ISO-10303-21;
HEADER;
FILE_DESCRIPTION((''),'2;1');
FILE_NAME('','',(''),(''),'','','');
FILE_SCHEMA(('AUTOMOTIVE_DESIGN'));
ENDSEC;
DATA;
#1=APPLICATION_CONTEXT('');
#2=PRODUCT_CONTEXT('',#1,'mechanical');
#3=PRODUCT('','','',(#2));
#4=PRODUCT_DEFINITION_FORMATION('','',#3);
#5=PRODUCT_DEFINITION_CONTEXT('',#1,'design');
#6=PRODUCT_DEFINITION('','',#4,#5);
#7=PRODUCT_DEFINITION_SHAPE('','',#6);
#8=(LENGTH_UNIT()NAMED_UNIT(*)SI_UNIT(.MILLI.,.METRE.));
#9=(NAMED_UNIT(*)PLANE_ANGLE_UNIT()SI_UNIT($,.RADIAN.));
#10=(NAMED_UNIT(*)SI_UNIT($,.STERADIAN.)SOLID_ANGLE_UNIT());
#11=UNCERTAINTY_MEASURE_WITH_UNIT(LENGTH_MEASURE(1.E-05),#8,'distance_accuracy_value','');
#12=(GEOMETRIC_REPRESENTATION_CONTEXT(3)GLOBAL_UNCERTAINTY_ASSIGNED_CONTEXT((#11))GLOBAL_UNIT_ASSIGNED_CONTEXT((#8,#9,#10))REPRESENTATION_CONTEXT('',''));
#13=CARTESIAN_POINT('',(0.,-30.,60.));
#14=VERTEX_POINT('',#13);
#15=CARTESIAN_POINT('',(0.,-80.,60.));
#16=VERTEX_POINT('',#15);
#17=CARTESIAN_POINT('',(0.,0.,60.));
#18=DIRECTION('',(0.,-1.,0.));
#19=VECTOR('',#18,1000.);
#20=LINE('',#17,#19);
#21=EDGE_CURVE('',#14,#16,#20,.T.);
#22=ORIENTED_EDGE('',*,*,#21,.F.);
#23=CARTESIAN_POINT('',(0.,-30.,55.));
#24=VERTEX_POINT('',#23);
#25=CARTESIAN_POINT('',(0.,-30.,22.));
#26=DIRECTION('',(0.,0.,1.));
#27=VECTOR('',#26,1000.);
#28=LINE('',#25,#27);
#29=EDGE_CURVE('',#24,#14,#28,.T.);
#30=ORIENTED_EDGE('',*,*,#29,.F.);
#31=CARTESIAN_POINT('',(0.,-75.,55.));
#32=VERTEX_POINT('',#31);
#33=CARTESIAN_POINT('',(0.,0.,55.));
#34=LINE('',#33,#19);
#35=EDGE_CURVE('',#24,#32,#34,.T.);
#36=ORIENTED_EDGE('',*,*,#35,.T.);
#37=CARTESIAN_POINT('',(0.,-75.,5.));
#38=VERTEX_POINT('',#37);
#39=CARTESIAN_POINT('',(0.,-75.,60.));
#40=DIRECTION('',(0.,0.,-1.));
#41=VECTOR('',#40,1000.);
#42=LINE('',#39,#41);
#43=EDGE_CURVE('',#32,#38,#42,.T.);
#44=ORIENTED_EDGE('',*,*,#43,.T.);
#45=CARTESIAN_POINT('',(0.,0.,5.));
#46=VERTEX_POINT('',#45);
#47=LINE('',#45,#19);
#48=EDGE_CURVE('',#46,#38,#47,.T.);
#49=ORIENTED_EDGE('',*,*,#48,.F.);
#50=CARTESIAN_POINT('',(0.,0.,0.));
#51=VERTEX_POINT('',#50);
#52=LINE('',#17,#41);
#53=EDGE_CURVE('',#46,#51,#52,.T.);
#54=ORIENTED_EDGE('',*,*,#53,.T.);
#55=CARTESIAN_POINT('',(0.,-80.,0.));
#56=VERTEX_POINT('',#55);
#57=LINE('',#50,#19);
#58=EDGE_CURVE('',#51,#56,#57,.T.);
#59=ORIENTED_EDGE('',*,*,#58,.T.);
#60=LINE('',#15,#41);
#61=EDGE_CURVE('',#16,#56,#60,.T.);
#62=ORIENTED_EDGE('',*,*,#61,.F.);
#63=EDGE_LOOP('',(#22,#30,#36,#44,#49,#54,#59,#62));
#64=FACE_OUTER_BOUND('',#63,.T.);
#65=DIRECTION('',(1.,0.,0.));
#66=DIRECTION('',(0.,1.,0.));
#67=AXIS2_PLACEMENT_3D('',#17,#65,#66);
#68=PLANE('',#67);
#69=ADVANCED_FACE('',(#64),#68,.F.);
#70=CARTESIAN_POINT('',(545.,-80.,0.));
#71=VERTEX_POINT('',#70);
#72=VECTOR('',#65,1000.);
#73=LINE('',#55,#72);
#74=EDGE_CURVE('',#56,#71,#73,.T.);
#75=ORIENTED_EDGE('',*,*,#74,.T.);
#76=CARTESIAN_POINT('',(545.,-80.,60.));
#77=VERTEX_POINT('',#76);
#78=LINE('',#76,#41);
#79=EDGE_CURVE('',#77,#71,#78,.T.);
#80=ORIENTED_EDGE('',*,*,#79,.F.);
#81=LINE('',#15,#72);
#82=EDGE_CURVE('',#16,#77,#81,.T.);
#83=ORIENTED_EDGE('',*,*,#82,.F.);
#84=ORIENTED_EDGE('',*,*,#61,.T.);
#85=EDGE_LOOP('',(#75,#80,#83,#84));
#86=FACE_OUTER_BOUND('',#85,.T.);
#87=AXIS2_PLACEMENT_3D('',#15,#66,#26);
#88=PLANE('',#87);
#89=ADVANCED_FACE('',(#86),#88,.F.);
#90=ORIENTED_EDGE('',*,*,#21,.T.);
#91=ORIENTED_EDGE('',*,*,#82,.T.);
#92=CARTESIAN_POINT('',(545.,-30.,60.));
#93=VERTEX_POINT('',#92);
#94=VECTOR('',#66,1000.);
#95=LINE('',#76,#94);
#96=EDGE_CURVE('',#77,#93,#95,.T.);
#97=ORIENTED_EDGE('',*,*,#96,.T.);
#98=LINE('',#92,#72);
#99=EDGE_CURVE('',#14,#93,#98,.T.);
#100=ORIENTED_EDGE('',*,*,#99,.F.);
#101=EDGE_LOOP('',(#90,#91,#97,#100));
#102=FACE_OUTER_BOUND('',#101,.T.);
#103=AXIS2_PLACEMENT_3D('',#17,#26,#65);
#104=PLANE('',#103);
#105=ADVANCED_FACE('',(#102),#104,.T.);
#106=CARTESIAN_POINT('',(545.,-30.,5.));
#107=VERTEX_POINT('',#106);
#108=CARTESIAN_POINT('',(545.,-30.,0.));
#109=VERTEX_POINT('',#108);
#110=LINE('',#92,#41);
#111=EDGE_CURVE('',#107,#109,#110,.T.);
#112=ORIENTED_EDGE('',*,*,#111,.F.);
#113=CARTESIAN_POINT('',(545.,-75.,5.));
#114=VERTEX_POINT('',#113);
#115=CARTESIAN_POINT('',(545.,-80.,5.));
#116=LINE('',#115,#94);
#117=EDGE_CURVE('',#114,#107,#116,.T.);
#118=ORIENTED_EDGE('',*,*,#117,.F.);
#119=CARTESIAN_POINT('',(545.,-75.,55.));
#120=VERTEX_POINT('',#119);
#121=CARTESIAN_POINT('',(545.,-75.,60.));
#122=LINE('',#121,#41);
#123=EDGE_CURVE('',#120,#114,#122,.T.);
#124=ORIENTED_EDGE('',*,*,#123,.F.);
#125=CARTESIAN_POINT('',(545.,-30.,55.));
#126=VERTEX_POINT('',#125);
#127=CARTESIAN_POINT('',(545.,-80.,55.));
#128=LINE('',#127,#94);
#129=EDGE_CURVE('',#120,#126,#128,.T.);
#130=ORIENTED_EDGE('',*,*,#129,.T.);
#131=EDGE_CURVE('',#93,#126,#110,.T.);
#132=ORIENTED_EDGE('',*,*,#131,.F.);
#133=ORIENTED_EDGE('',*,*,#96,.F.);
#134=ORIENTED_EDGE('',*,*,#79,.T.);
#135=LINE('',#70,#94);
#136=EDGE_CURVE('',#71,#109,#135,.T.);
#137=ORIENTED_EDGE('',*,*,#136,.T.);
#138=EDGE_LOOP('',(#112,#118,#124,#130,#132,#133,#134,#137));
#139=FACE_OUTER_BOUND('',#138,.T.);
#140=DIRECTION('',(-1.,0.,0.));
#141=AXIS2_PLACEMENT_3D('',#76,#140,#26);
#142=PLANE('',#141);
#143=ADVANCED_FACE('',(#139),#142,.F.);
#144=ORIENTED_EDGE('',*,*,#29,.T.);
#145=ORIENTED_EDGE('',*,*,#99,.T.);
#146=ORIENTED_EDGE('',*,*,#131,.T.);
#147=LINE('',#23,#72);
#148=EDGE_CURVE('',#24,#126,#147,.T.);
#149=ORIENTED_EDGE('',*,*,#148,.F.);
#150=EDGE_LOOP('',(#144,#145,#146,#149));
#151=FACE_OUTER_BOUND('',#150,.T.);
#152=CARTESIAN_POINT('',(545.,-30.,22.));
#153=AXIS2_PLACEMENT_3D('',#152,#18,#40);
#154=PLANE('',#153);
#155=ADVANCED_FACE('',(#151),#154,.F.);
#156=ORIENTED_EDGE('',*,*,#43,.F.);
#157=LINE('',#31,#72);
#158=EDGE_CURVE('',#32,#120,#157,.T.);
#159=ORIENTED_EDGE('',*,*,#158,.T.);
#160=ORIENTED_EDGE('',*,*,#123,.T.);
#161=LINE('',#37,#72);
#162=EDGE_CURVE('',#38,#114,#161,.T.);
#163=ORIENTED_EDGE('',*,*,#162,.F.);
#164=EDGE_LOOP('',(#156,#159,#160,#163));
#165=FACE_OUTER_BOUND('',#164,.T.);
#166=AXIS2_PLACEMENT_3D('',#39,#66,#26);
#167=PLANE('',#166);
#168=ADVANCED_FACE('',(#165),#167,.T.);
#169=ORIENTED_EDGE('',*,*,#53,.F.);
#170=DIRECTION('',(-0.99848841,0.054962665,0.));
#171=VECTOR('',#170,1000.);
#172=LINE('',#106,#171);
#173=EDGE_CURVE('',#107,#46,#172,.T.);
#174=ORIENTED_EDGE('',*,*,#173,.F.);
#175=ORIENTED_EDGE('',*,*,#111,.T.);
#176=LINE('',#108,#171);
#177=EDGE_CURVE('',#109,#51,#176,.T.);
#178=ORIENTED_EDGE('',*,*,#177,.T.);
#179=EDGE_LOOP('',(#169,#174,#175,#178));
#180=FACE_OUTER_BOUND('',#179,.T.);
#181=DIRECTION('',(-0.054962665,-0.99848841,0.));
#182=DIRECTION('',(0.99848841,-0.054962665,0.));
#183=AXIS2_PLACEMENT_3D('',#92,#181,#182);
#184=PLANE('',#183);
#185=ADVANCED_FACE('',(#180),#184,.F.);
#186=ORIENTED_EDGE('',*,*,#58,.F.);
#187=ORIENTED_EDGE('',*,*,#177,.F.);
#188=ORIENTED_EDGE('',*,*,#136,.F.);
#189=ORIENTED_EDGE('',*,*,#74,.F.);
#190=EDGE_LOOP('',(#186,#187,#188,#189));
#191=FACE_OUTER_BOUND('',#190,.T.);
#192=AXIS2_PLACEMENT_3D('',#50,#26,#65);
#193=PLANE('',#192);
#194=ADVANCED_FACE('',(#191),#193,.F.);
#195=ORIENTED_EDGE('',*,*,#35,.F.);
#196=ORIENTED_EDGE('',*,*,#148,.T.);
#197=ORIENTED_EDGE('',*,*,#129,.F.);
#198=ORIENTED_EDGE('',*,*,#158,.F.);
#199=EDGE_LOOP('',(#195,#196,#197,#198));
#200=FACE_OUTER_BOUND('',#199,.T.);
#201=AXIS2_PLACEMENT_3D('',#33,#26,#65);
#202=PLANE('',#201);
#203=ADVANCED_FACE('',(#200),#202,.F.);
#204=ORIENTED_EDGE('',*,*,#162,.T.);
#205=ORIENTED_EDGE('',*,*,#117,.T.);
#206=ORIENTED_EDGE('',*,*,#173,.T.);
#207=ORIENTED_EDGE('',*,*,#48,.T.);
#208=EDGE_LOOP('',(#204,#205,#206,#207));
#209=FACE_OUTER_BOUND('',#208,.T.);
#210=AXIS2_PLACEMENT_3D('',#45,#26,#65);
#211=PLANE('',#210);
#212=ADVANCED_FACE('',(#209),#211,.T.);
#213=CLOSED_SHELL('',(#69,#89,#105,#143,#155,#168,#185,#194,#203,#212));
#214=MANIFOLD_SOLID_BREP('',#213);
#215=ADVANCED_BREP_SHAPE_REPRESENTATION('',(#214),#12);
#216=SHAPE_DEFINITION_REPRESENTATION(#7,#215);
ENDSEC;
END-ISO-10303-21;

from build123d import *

# Parameters (mm, degrees)
EXTRUDE_1_DEPTH     = 60
SHELL_2_T           = -5
CUT_EXTRUDE_2_DEPTH = 38


with BuildPart() as part:
    # 草图1 → 凸台-拉伸1 (new body)
    with BuildSketch(Plane.XY):
        Polygon((0, 0), (0, -80), (545, -80), (545, -30), align=None)
    extrude(amount=EXTRUDE_1_DEPTH)

    # 抽壳2
    shell_2_openings = [part.faces().sort_by_distance(p)[0] for p in [
        (545, -55, 30),
        (0, -40, 30),
        (272.5, -15, 30),
    ]]
    offset(amount=SHELL_2_T, openings=shell_2_openings, kind=Kind.INTERSECTION)

    # 草图4 → 切除-拉伸2 (cut)
    with BuildSketch(Plane.XY.offset(60)):
        Polygon((545, -30), (0, -30), (0, 50.034428037), align=None)
    extrude(amount=-CUT_EXTRUDE_2_DEPTH, mode=Mode.SUBTRACT)


solid = part.part
